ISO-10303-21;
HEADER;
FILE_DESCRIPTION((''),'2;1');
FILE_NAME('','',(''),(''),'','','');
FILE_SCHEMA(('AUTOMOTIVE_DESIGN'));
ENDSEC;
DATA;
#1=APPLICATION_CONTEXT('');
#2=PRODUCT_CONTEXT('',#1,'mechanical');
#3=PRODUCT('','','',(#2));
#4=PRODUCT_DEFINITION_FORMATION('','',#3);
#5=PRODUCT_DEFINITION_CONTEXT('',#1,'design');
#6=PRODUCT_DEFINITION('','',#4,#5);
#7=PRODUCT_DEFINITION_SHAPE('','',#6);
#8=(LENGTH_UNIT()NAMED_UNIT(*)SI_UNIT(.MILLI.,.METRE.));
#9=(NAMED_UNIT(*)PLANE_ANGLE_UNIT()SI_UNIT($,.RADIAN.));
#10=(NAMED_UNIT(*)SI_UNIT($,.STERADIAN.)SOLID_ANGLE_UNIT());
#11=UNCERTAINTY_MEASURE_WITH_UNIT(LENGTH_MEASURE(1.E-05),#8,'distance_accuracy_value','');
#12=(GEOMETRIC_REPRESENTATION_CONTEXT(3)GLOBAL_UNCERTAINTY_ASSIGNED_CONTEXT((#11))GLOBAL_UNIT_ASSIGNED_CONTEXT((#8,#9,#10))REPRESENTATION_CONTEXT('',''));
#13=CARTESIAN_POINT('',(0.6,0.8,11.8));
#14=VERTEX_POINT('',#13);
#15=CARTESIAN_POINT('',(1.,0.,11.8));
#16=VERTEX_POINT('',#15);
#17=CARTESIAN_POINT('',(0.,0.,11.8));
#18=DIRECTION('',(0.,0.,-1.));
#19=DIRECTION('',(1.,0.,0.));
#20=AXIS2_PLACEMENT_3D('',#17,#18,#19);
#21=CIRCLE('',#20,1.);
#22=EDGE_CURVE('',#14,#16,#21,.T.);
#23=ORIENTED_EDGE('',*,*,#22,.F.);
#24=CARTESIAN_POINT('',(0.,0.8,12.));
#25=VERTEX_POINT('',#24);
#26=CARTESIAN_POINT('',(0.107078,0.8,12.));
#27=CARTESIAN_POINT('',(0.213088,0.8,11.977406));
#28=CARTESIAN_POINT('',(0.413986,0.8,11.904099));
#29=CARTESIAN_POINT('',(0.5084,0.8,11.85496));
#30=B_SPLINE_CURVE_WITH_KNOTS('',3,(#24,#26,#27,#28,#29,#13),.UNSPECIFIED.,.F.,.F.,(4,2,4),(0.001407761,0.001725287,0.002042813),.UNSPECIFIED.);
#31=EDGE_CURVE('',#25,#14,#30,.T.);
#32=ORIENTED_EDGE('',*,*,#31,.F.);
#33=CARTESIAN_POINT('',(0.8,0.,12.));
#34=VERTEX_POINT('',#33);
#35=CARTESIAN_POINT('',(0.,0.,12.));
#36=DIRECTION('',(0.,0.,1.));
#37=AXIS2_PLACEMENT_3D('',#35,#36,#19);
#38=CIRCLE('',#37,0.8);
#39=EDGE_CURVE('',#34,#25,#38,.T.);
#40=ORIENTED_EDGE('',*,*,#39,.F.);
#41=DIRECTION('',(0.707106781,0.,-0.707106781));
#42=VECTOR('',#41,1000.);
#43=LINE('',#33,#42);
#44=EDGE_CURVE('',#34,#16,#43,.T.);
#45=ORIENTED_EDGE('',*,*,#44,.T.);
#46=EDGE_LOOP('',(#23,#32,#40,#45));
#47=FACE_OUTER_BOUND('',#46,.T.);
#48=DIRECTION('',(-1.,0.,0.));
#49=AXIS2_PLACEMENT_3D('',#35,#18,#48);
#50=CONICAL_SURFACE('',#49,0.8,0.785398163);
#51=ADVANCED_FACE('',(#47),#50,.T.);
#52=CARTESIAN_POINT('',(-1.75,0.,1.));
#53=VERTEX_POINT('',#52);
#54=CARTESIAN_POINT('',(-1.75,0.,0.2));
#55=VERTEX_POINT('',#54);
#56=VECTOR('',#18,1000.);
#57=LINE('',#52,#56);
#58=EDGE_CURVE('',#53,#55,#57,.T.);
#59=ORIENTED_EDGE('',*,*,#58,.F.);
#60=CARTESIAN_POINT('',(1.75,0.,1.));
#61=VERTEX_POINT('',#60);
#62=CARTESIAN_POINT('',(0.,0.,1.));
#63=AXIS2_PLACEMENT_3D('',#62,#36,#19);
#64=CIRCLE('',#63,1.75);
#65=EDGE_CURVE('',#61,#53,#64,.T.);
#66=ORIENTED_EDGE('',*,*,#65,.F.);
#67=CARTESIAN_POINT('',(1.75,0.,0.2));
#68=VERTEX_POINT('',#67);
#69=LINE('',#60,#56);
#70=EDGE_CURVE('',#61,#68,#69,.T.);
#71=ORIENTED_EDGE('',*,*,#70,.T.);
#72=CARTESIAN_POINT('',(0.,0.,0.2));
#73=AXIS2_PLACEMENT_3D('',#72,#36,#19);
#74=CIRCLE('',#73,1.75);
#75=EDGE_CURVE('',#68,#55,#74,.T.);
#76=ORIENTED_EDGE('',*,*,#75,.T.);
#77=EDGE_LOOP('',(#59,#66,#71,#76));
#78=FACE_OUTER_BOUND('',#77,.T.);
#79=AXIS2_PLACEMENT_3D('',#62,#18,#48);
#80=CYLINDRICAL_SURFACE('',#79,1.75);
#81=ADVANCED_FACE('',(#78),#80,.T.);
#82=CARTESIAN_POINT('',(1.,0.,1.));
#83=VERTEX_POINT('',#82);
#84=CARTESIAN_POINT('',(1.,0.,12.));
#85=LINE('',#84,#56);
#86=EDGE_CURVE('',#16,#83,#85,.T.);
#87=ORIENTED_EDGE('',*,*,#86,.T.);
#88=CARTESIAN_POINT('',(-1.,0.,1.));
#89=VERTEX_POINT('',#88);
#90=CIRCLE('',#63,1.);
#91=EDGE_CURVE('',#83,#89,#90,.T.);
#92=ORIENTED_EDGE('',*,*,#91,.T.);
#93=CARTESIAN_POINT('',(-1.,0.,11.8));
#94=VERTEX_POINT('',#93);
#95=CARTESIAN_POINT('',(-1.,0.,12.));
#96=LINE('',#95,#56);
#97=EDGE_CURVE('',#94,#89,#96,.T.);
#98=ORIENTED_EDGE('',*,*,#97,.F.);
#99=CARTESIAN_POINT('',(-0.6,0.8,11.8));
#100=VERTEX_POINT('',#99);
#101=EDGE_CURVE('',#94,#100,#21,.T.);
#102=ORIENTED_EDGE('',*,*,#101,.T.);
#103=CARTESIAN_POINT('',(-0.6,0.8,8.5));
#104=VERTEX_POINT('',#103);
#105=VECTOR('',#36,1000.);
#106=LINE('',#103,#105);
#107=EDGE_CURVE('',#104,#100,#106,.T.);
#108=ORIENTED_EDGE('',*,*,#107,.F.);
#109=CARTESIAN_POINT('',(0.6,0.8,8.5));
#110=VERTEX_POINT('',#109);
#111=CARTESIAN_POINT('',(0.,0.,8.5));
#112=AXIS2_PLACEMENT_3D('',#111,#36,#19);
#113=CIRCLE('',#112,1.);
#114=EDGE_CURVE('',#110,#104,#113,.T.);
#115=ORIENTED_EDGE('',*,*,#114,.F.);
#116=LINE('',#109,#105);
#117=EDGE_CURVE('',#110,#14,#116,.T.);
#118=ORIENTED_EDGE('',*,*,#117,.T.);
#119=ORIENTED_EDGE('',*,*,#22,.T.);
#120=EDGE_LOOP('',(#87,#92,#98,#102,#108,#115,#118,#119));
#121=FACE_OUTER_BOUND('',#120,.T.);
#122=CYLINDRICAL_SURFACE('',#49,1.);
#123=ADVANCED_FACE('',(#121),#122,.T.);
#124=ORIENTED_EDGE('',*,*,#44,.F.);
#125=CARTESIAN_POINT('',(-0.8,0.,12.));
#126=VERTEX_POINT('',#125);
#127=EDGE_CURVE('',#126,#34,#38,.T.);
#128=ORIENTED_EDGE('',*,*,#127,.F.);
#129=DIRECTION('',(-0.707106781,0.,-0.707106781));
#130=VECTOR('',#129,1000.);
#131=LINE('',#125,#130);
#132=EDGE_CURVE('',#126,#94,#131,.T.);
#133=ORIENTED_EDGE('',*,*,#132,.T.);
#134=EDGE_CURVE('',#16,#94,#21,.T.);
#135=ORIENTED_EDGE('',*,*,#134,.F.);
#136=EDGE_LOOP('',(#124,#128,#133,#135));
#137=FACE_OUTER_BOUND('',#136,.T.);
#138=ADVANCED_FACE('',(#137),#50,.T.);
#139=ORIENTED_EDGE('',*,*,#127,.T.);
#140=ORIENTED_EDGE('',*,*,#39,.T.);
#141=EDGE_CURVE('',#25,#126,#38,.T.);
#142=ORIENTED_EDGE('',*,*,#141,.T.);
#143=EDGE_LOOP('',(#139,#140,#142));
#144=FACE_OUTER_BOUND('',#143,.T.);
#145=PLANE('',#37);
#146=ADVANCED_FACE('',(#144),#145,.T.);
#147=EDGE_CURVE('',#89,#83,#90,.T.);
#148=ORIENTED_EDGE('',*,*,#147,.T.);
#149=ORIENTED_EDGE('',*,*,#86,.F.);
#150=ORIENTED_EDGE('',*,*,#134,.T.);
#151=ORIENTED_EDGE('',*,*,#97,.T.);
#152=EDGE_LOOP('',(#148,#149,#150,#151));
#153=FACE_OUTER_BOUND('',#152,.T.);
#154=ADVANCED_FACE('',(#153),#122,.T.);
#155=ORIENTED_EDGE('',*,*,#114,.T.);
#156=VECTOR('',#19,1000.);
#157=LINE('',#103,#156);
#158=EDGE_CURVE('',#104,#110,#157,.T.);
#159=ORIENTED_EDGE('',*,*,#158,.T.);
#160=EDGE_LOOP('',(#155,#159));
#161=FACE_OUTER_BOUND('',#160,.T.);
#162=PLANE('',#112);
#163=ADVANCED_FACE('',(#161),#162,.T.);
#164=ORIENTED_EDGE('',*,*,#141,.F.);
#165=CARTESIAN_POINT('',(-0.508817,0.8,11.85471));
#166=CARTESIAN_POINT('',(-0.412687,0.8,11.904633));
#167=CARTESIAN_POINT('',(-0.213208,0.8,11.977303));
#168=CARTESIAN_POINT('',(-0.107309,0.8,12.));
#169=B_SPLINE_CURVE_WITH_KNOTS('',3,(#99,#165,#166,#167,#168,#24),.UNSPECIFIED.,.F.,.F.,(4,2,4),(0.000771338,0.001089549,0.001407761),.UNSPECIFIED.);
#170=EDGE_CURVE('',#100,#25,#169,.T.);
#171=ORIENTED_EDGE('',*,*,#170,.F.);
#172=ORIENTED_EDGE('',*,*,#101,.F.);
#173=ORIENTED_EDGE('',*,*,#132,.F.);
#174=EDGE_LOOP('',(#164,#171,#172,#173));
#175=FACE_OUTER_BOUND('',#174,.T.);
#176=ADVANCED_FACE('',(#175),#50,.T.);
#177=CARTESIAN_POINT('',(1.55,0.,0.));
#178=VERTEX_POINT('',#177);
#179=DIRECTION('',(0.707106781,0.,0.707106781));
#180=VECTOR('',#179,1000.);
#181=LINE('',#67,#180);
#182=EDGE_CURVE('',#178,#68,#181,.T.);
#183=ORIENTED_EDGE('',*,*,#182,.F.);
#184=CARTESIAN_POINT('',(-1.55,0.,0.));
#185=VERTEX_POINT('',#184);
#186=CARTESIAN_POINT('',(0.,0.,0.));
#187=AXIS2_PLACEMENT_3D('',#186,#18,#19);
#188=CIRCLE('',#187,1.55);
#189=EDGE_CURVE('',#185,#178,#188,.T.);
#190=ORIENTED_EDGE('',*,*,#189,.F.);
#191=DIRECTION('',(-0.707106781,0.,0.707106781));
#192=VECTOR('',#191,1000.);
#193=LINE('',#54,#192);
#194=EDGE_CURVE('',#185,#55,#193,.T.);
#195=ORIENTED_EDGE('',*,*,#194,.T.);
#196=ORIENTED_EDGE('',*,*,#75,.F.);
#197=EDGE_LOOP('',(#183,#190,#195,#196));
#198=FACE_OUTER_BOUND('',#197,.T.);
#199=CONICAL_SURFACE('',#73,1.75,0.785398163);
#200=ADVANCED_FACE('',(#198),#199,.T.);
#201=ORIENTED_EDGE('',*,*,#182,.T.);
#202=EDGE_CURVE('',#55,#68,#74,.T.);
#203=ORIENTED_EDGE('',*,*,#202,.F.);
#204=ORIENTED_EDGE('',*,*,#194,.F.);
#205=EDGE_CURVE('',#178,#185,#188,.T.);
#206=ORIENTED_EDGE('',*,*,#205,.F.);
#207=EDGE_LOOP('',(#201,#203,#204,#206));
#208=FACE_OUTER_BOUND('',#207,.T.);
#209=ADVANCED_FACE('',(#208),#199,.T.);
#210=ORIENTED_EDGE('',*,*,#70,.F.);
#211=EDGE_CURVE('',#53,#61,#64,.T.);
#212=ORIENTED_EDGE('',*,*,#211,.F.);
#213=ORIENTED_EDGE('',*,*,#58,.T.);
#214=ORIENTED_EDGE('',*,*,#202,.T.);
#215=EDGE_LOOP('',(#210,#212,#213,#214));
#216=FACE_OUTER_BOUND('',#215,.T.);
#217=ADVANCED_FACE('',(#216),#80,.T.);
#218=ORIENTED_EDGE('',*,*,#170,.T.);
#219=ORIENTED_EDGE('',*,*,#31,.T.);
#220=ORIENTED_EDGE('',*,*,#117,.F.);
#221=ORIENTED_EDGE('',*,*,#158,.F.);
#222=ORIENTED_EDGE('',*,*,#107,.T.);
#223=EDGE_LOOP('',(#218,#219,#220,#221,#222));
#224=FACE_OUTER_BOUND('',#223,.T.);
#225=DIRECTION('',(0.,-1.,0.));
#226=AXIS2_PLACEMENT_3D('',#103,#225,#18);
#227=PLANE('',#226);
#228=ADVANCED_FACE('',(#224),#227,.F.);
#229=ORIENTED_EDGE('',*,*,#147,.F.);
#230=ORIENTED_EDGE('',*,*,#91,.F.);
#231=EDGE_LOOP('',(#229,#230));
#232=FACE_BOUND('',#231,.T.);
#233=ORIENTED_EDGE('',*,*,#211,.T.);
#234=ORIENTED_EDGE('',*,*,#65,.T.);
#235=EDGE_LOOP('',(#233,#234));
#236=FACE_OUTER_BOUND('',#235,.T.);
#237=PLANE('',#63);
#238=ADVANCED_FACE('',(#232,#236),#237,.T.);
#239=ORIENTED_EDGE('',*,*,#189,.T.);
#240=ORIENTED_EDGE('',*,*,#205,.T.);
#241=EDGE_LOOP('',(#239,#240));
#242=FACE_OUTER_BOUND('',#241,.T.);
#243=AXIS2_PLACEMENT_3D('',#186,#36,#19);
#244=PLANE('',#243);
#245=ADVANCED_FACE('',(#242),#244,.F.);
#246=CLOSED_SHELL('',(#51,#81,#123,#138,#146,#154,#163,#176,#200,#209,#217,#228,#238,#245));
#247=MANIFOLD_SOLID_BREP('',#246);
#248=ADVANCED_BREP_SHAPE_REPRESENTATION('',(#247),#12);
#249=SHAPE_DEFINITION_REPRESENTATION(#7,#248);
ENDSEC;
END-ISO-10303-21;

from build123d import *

# Parameters (mm, degrees)
SKETCH1_R           = 1.75
BOSS_EXTRUDE1_DEPTH = 1
SKETCH2_R           = 1
BOSS_EXTRUDE2_DEPTH = 11
CHAMFER1_SIZE       = 0.2
CUT_EXTRUDE1_START  = -3.5
CUT_EXTRUDE1_DEPTH  = 3.5


with BuildPart() as part:
    # Sketch1 → Boss-Extrude1 (new body)
    with BuildSketch(Plane.XY):
        Circle(SKETCH1_R)
    extrude(amount=BOSS_EXTRUDE1_DEPTH)

    # Sketch2 → Boss-Extrude2 (add)
    with BuildSketch(Plane.XY.offset(1)):
        Circle(SKETCH2_R)
    extrude(amount=BOSS_EXTRUDE2_DEPTH)

    # Chamfer1
    chamfer1_edges = [part.edges().sort_by_distance(p)[0] for p in [
        (-1.75, 0, 0),
        (-1, 0, 12),
    ]]
    chamfer(chamfer1_edges, length=CHAMFER1_SIZE)

    # Sketch3 → Cut-Extrude1 (cut)
    with BuildSketch(Plane.XY.offset(12).offset(CUT_EXTRUDE1_START)):
        with BuildLine():
            Line((-0.6, 0.8), (0.6, 0.8))
            ThreePointArc((0.6, 0.8), (0, 1), (-0.6, 0.8))
        make_face()
    extrude(amount=CUT_EXTRUDE1_DEPTH, mode=Mode.SUBTRACT)


solid = part.part
